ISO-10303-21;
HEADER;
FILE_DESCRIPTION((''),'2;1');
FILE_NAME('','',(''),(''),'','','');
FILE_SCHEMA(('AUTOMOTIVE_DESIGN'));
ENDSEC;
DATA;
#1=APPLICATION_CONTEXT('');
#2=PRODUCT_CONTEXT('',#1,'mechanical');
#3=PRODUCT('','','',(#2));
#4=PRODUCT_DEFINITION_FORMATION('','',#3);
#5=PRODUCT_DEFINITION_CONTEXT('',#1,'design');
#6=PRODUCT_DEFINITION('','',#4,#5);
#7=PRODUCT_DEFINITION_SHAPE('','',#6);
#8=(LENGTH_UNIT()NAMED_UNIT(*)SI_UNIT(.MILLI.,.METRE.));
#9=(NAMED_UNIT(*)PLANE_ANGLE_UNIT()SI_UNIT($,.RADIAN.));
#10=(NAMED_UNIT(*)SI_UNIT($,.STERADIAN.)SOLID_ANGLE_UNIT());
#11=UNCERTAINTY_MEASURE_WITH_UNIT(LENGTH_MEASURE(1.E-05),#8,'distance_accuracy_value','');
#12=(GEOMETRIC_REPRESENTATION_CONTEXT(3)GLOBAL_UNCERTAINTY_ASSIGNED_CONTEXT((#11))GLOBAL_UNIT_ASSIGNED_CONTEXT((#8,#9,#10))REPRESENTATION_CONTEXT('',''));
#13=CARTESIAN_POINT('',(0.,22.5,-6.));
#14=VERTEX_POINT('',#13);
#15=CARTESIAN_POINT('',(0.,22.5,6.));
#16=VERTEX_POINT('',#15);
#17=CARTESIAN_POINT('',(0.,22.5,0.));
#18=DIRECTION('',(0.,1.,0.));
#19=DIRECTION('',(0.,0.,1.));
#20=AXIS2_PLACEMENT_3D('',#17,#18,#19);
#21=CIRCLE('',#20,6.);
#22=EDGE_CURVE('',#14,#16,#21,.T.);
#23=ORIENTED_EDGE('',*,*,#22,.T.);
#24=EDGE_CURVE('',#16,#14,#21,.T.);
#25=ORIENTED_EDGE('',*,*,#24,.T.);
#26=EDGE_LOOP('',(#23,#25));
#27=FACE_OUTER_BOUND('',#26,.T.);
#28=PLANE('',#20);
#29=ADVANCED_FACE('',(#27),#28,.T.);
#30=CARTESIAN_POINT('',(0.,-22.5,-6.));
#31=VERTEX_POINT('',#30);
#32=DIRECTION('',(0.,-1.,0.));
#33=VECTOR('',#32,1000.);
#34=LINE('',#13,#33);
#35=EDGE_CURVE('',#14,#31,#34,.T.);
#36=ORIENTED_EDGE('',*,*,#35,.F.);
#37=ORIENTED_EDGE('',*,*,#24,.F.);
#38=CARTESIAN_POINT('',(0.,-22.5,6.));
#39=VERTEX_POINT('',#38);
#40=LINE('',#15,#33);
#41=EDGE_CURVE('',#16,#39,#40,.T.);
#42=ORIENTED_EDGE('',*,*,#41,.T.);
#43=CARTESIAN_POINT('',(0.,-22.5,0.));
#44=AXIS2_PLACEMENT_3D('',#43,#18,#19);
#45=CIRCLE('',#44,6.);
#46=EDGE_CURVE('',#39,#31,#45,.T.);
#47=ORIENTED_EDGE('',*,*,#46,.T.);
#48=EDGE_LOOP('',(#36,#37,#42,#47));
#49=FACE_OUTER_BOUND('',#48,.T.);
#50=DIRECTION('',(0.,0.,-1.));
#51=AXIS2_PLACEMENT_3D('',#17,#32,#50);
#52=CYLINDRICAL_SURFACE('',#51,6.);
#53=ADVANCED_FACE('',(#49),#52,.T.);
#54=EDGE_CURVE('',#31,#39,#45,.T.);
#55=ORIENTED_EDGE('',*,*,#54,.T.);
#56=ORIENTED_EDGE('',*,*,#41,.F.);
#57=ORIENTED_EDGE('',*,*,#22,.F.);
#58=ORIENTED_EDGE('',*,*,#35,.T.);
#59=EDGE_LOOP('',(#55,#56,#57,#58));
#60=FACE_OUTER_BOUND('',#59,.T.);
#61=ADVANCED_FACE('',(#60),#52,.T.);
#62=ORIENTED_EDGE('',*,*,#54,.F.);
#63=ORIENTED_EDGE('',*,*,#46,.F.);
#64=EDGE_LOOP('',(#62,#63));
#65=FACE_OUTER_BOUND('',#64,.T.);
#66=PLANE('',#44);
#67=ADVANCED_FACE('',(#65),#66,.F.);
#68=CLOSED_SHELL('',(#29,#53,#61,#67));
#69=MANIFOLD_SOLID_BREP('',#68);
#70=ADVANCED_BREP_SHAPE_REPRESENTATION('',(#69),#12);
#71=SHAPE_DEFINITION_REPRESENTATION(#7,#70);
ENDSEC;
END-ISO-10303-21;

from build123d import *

# Parameters (mm, degrees)
SHANK_PROFILE_12_R = 6
SHANK_12X45_DEPTH  = 22.5


with BuildPart() as part:
    # Shank Profile Ø12 → Shank Ø12x45 (new, symmetric)
    with BuildSketch(Plane(origin=(0, 0, 0), x_dir=(1, 0, 0), z_dir=(0, 1, 0))):
        with Locations(Location((0, 0, 0), (0, 0, 90))):
            Circle(SHANK_PROFILE_12_R)
    extrude(amount=SHANK_12X45_DEPTH, both=True)


solid = part.part
